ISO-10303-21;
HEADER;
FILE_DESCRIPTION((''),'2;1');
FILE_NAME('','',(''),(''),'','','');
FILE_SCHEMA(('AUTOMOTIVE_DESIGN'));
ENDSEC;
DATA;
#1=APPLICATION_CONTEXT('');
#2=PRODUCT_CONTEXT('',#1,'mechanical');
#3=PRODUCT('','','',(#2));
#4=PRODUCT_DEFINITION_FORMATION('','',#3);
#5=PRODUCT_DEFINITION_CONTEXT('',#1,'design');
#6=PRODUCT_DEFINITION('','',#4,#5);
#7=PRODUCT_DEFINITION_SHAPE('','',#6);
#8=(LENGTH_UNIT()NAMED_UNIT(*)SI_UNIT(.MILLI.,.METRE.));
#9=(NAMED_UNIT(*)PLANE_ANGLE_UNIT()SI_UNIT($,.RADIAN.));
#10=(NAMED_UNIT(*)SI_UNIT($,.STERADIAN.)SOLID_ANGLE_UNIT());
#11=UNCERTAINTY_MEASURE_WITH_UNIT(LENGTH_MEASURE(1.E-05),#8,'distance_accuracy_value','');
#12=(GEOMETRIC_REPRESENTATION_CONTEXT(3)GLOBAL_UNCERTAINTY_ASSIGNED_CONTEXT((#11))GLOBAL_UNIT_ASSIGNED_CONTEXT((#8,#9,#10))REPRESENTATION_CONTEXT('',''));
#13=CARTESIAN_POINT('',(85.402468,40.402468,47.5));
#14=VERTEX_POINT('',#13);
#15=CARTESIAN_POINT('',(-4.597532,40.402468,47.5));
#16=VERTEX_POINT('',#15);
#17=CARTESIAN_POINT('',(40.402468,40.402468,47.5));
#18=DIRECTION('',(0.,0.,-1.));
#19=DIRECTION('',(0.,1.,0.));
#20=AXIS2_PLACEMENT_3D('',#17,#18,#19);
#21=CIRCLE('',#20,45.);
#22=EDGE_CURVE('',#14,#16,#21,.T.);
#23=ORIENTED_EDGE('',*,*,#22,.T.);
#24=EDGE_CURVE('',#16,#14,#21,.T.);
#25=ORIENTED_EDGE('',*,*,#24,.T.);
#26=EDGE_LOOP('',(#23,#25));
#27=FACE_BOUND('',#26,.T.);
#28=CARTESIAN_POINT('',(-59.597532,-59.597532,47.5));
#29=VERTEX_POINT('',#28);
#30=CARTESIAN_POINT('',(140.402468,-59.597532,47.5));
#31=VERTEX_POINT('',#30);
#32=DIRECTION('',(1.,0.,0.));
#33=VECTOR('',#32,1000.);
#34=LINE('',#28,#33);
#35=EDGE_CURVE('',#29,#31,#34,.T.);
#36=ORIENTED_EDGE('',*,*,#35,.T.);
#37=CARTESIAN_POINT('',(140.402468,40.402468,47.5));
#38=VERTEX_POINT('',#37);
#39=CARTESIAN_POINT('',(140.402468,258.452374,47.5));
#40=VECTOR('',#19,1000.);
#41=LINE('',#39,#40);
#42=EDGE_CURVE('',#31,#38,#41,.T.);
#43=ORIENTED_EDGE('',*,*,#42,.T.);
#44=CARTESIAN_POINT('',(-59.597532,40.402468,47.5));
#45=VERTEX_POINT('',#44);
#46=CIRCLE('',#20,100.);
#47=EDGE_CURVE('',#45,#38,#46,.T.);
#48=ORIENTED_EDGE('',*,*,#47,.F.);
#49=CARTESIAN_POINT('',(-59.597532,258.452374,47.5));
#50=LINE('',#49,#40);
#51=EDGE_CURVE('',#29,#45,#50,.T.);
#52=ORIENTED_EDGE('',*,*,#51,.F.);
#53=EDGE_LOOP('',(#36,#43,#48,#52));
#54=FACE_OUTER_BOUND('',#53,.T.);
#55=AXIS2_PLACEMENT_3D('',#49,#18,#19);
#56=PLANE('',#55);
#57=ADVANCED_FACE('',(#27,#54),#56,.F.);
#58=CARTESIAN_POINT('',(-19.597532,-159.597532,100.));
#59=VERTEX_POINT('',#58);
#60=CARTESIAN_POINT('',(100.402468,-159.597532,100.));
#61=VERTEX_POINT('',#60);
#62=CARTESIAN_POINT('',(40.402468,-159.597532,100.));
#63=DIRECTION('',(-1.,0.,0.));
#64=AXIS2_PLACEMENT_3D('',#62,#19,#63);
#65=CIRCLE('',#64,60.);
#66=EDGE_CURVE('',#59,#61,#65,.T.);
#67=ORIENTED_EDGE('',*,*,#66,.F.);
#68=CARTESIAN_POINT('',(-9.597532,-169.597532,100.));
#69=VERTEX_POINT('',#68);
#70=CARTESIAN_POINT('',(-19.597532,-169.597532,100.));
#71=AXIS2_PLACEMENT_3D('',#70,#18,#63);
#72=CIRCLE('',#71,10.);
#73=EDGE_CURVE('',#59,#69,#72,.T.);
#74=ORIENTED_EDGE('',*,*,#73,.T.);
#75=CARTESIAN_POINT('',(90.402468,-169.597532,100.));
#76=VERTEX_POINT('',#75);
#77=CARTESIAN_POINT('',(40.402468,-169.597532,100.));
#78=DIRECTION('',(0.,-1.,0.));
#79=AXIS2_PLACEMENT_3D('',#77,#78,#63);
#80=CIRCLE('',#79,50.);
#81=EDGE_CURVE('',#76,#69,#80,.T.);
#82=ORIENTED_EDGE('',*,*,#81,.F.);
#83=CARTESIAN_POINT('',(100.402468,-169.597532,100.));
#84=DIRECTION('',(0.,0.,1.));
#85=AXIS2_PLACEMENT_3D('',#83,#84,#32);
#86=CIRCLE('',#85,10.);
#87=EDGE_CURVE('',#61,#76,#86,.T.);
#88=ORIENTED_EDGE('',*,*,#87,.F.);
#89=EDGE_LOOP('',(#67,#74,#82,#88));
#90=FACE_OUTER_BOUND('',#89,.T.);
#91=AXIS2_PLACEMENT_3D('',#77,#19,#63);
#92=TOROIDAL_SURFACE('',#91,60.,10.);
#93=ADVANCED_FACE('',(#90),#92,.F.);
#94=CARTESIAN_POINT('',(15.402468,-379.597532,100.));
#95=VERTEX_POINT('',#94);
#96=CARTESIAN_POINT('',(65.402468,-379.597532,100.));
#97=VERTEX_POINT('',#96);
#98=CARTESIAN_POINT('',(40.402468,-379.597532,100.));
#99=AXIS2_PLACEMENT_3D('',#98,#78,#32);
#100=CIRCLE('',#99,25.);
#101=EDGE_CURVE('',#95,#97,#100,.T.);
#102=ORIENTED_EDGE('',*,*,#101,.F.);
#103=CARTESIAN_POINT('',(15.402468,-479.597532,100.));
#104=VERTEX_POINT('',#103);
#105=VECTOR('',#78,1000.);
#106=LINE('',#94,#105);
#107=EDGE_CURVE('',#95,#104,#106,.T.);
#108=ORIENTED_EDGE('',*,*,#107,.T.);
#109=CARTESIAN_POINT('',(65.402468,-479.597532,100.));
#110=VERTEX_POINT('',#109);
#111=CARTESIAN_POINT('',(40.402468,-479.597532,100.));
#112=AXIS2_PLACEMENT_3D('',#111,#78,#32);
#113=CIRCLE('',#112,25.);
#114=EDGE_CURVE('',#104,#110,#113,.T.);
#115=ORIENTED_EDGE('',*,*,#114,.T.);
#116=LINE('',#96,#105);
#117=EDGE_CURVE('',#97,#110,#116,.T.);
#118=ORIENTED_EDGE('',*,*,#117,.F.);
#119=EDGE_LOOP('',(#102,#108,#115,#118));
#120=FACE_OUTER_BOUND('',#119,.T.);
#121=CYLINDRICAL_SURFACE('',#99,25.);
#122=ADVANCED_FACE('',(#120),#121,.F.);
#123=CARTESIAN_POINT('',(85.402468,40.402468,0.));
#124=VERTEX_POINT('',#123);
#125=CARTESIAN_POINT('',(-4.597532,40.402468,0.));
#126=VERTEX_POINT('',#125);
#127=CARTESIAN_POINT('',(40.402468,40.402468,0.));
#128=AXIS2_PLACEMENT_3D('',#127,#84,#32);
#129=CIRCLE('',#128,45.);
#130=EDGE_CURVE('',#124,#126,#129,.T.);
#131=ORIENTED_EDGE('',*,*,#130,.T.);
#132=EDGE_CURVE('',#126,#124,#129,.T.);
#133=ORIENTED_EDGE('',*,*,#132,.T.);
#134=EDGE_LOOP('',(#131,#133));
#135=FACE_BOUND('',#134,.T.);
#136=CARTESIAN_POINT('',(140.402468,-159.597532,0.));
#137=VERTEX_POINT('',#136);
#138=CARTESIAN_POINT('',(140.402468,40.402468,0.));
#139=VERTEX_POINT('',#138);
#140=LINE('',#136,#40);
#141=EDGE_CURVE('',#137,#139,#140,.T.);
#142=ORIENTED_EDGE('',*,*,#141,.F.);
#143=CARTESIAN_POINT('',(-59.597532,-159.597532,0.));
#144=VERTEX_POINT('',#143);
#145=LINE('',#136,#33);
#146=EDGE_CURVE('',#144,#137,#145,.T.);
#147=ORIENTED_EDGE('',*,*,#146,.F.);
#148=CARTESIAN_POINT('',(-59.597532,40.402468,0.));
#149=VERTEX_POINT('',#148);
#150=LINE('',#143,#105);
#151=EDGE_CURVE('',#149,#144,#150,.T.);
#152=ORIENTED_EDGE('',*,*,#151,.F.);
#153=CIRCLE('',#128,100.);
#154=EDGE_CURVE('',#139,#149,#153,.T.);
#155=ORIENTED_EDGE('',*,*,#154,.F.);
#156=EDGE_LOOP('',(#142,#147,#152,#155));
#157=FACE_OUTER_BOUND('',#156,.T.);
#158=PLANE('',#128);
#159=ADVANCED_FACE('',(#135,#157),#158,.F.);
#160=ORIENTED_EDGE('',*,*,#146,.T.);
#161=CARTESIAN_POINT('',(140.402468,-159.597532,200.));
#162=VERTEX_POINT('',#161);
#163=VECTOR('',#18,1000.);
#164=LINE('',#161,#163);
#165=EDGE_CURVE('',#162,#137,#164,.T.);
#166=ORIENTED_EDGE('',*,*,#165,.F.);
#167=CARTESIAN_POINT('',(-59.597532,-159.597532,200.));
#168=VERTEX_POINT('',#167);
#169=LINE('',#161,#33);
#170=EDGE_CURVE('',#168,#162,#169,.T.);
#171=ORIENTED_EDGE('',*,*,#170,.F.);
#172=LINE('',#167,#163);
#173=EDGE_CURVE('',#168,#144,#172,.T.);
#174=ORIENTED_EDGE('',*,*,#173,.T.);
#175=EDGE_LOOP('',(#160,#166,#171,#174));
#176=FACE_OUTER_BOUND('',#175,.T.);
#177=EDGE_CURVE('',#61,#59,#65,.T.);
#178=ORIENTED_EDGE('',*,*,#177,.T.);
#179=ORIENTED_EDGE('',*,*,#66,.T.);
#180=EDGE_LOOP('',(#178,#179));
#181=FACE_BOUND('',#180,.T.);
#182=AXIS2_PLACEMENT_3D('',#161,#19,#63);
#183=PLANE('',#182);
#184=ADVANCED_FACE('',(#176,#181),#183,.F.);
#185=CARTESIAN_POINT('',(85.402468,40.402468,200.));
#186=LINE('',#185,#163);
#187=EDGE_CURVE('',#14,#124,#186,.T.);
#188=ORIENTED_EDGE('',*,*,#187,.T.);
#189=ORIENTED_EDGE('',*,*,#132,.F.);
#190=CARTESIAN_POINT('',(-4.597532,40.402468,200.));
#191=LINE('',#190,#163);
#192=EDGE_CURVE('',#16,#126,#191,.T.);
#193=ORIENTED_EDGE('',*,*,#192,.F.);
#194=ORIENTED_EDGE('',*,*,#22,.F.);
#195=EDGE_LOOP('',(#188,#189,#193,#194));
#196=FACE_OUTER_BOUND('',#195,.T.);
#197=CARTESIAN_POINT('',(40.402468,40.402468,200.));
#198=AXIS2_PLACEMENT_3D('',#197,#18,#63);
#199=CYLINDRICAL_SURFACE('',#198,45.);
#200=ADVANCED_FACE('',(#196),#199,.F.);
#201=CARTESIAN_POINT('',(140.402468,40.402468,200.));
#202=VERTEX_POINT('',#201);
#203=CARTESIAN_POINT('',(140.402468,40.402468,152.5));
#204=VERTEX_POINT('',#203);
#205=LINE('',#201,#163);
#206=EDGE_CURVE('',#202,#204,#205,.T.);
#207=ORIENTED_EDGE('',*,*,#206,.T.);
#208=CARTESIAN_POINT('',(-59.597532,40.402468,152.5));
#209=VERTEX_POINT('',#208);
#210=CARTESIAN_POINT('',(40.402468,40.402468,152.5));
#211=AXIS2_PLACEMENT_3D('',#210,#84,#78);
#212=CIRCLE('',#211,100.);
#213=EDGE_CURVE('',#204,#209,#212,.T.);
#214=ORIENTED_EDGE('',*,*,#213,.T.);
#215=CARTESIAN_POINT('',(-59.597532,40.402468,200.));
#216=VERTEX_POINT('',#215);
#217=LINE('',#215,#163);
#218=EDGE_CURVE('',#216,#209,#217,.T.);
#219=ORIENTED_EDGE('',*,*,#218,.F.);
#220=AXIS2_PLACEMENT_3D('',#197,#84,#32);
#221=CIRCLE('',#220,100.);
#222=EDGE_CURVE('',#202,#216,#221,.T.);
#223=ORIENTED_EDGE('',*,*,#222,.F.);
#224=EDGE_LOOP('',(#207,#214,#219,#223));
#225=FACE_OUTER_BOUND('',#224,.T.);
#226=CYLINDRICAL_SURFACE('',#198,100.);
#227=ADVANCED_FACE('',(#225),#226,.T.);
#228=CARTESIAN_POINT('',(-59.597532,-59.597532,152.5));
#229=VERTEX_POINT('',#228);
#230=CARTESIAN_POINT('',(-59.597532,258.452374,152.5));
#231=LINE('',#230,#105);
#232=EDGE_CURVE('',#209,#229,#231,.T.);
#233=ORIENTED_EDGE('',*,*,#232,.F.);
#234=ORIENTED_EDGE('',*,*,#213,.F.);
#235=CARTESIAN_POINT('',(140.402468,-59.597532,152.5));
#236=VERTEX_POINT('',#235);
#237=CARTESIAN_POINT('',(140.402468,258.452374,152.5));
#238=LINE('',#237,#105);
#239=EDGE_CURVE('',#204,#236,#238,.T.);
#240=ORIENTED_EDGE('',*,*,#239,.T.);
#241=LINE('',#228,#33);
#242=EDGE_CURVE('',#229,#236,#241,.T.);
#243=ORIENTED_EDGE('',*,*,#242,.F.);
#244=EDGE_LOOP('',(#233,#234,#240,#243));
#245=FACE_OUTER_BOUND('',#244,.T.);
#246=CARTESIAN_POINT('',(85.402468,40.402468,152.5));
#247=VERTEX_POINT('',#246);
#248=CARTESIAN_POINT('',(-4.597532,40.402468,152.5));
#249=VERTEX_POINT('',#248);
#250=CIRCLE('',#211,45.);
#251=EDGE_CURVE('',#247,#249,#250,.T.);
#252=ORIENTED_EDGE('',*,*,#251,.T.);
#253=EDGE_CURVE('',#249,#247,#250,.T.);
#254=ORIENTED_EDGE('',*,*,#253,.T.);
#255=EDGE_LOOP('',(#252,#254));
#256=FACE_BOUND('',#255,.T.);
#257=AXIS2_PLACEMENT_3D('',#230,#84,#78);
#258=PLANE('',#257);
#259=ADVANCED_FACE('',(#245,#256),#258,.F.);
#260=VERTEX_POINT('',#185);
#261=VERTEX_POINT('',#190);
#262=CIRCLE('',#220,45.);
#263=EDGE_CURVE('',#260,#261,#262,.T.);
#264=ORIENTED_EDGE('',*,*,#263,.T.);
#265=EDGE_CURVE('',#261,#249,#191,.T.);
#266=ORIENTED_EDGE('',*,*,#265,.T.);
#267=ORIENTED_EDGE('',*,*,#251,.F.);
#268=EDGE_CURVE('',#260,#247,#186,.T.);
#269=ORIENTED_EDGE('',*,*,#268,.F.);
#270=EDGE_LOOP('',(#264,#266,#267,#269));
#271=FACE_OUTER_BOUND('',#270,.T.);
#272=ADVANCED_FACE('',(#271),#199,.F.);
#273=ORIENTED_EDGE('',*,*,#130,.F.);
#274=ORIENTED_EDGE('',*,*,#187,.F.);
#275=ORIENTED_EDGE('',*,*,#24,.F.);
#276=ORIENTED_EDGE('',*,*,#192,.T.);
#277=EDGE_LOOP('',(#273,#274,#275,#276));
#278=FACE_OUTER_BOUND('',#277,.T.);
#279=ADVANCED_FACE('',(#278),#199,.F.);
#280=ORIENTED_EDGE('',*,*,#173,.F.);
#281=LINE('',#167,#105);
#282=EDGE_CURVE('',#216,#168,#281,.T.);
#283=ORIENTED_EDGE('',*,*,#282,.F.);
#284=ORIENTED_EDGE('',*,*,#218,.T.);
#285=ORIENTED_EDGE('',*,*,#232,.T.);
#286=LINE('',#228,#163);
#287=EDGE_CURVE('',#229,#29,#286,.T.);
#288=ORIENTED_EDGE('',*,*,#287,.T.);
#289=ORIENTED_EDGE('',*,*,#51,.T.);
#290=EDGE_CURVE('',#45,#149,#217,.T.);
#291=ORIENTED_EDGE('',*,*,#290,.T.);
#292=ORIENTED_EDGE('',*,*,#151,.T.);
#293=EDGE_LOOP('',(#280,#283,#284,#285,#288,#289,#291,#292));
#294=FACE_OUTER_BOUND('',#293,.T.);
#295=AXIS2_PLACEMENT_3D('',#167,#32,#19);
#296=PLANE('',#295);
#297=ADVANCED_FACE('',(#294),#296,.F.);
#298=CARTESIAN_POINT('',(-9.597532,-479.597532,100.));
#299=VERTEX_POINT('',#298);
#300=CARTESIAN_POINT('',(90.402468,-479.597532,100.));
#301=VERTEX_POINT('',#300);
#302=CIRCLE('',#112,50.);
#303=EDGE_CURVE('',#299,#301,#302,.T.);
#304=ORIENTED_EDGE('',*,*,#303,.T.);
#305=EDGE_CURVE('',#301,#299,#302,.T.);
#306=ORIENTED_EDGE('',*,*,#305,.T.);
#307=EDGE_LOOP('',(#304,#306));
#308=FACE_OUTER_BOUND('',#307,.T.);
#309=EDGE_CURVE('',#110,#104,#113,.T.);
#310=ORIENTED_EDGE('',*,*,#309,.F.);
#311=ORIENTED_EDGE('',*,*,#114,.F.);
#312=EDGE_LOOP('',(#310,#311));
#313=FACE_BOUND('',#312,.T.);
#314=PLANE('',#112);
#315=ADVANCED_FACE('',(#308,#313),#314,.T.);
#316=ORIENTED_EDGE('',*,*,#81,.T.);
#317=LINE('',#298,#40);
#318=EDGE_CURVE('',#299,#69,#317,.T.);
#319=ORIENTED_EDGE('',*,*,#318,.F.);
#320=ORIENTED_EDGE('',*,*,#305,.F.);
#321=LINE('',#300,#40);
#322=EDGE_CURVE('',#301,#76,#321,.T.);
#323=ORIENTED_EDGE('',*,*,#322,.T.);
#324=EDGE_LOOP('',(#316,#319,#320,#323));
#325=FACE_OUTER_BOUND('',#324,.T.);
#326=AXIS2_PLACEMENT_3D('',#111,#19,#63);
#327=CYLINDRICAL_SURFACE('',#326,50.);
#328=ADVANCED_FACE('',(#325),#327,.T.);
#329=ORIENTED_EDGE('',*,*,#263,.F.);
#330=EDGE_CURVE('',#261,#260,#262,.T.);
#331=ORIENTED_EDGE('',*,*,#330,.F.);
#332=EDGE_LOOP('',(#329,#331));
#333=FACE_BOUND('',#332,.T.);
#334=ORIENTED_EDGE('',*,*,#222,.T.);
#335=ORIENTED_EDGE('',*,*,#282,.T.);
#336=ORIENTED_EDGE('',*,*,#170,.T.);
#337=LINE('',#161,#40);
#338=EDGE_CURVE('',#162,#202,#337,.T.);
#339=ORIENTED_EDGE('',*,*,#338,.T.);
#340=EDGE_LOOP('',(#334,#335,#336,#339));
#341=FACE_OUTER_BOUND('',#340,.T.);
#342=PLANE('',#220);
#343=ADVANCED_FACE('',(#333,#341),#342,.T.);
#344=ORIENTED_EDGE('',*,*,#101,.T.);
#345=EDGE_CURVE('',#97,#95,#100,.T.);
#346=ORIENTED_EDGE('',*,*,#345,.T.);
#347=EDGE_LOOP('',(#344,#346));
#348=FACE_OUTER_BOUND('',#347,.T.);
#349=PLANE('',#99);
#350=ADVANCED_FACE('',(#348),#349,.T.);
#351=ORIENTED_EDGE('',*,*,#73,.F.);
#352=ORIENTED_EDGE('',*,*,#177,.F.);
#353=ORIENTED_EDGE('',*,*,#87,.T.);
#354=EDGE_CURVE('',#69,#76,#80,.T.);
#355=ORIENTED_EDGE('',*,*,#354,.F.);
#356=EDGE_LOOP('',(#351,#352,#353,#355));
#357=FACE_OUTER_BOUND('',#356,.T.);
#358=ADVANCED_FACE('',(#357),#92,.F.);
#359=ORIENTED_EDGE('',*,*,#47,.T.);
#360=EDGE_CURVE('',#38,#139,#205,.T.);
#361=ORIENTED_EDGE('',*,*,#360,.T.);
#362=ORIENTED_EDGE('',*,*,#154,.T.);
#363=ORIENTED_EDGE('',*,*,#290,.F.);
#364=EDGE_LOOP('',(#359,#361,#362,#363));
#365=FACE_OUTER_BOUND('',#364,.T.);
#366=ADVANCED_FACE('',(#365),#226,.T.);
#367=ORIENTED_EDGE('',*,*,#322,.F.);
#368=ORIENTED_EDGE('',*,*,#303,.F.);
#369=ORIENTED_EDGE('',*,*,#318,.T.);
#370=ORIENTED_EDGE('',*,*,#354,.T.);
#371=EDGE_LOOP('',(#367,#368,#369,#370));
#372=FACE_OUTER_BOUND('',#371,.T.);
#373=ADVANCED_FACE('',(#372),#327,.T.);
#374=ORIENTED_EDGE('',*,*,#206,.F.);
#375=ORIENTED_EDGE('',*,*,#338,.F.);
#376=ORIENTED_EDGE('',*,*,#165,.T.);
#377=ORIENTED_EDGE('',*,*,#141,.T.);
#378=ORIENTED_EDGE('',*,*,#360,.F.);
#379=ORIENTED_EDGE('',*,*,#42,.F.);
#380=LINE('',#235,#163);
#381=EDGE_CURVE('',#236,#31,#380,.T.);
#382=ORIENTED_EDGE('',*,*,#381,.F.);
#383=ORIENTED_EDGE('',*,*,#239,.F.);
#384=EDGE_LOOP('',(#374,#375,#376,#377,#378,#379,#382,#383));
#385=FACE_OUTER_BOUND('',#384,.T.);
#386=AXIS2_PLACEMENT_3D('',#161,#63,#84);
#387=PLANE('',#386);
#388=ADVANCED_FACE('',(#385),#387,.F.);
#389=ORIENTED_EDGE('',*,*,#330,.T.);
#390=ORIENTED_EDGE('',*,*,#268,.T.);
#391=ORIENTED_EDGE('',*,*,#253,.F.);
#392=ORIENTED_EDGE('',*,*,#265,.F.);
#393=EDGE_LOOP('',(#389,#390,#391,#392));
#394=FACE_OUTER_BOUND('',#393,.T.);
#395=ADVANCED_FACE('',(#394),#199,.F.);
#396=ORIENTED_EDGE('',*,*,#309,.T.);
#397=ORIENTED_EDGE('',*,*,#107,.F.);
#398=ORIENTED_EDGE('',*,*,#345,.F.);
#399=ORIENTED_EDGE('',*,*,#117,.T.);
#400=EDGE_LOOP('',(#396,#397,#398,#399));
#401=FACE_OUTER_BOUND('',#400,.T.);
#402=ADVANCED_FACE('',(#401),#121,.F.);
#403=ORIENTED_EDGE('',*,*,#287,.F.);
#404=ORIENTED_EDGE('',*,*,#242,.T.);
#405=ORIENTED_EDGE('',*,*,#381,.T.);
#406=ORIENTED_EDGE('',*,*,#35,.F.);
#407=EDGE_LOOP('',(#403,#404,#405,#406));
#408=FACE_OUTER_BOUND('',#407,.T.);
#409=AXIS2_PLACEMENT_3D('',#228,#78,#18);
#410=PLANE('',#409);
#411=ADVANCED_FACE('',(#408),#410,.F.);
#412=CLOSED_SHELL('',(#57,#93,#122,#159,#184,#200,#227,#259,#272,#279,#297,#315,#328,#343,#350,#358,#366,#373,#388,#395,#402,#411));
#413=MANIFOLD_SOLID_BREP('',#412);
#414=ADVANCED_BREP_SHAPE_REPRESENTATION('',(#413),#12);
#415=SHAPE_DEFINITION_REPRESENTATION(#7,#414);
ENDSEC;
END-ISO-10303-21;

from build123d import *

# Parameters (mm, degrees)
SKETCH1_R           = 45
BOSS_EXTRUDE2_DEPTH = 200
SKETCH2_W           = 105
SKETCH2_H           = 318.049906591
CUT_EXTRUDE1_DEPTH  = 325.763563649
SKETCH3_R           = 50
BOSS_EXTRUDE3_DEPTH = 320
SKETCH4_R           = 25
CUT_EXTRUDE2_DEPTH  = 100
FILLET1_R           = 10


with BuildPart() as part:
    # Sketch1 → Boss-Extrude2 (new body)
    with BuildSketch(Plane.XY):
        with BuildLine():
            Line((140.402467833, -159.597532167), (-59.597532167, -159.597532167))
            Line((-59.597532167, -159.597532167), (-59.597532167, 40.402467833))
            ThreePointArc((-59.597532167, 40.402467833), (40.402467833, 140.402467833), (140.402467833, 40.402467833))
            Line((140.402467833, 40.402467833), (140.402467833, -159.597532167))
        make_face()
        with Locations((40.402467833, 40.402467833)):
            Circle(SKETCH1_R, mode=Mode.SUBTRACT)
    extrude(amount=BOSS_EXTRUDE2_DEPTH)

    # Sketch2 → Cut-Extrude1 (cut, through all)
    with BuildSketch(Plane(origin=(140.402467833, 0, 0), x_dir=(0, 0, -1), z_dir=(1, 0, 0))):
        with Locations((-100, 99.427421129)):
            Rectangle(SKETCH2_W, SKETCH2_H)
    extrude(amount=-CUT_EXTRUDE1_DEPTH, mode=Mode.SUBTRACT)

    # Sketch3 → Boss-Extrude3 (add)
    with BuildSketch(Plane.XZ.offset(159.597532167)):
        with Locations((40.402467833, 100)):
            Circle(SKETCH3_R)
    extrude(amount=BOSS_EXTRUDE3_DEPTH)

    # Sketch4 → Cut-Extrude2 (cut)
    with BuildSketch(Plane.XZ.offset(479.597532167)):
        with Locations((40.402467833, 100)):
            Circle(SKETCH4_R)
    extrude(amount=-CUT_EXTRUDE2_DEPTH, mode=Mode.SUBTRACT)

    # Fillet1
    fillet1_edges = [part.edges().sort_by_distance(p)[0] for p in [
        (-9.597532167, -159.597532167, 100),
    ]]
    fillet(fillet1_edges, radius=FILLET1_R)


solid = part.part
